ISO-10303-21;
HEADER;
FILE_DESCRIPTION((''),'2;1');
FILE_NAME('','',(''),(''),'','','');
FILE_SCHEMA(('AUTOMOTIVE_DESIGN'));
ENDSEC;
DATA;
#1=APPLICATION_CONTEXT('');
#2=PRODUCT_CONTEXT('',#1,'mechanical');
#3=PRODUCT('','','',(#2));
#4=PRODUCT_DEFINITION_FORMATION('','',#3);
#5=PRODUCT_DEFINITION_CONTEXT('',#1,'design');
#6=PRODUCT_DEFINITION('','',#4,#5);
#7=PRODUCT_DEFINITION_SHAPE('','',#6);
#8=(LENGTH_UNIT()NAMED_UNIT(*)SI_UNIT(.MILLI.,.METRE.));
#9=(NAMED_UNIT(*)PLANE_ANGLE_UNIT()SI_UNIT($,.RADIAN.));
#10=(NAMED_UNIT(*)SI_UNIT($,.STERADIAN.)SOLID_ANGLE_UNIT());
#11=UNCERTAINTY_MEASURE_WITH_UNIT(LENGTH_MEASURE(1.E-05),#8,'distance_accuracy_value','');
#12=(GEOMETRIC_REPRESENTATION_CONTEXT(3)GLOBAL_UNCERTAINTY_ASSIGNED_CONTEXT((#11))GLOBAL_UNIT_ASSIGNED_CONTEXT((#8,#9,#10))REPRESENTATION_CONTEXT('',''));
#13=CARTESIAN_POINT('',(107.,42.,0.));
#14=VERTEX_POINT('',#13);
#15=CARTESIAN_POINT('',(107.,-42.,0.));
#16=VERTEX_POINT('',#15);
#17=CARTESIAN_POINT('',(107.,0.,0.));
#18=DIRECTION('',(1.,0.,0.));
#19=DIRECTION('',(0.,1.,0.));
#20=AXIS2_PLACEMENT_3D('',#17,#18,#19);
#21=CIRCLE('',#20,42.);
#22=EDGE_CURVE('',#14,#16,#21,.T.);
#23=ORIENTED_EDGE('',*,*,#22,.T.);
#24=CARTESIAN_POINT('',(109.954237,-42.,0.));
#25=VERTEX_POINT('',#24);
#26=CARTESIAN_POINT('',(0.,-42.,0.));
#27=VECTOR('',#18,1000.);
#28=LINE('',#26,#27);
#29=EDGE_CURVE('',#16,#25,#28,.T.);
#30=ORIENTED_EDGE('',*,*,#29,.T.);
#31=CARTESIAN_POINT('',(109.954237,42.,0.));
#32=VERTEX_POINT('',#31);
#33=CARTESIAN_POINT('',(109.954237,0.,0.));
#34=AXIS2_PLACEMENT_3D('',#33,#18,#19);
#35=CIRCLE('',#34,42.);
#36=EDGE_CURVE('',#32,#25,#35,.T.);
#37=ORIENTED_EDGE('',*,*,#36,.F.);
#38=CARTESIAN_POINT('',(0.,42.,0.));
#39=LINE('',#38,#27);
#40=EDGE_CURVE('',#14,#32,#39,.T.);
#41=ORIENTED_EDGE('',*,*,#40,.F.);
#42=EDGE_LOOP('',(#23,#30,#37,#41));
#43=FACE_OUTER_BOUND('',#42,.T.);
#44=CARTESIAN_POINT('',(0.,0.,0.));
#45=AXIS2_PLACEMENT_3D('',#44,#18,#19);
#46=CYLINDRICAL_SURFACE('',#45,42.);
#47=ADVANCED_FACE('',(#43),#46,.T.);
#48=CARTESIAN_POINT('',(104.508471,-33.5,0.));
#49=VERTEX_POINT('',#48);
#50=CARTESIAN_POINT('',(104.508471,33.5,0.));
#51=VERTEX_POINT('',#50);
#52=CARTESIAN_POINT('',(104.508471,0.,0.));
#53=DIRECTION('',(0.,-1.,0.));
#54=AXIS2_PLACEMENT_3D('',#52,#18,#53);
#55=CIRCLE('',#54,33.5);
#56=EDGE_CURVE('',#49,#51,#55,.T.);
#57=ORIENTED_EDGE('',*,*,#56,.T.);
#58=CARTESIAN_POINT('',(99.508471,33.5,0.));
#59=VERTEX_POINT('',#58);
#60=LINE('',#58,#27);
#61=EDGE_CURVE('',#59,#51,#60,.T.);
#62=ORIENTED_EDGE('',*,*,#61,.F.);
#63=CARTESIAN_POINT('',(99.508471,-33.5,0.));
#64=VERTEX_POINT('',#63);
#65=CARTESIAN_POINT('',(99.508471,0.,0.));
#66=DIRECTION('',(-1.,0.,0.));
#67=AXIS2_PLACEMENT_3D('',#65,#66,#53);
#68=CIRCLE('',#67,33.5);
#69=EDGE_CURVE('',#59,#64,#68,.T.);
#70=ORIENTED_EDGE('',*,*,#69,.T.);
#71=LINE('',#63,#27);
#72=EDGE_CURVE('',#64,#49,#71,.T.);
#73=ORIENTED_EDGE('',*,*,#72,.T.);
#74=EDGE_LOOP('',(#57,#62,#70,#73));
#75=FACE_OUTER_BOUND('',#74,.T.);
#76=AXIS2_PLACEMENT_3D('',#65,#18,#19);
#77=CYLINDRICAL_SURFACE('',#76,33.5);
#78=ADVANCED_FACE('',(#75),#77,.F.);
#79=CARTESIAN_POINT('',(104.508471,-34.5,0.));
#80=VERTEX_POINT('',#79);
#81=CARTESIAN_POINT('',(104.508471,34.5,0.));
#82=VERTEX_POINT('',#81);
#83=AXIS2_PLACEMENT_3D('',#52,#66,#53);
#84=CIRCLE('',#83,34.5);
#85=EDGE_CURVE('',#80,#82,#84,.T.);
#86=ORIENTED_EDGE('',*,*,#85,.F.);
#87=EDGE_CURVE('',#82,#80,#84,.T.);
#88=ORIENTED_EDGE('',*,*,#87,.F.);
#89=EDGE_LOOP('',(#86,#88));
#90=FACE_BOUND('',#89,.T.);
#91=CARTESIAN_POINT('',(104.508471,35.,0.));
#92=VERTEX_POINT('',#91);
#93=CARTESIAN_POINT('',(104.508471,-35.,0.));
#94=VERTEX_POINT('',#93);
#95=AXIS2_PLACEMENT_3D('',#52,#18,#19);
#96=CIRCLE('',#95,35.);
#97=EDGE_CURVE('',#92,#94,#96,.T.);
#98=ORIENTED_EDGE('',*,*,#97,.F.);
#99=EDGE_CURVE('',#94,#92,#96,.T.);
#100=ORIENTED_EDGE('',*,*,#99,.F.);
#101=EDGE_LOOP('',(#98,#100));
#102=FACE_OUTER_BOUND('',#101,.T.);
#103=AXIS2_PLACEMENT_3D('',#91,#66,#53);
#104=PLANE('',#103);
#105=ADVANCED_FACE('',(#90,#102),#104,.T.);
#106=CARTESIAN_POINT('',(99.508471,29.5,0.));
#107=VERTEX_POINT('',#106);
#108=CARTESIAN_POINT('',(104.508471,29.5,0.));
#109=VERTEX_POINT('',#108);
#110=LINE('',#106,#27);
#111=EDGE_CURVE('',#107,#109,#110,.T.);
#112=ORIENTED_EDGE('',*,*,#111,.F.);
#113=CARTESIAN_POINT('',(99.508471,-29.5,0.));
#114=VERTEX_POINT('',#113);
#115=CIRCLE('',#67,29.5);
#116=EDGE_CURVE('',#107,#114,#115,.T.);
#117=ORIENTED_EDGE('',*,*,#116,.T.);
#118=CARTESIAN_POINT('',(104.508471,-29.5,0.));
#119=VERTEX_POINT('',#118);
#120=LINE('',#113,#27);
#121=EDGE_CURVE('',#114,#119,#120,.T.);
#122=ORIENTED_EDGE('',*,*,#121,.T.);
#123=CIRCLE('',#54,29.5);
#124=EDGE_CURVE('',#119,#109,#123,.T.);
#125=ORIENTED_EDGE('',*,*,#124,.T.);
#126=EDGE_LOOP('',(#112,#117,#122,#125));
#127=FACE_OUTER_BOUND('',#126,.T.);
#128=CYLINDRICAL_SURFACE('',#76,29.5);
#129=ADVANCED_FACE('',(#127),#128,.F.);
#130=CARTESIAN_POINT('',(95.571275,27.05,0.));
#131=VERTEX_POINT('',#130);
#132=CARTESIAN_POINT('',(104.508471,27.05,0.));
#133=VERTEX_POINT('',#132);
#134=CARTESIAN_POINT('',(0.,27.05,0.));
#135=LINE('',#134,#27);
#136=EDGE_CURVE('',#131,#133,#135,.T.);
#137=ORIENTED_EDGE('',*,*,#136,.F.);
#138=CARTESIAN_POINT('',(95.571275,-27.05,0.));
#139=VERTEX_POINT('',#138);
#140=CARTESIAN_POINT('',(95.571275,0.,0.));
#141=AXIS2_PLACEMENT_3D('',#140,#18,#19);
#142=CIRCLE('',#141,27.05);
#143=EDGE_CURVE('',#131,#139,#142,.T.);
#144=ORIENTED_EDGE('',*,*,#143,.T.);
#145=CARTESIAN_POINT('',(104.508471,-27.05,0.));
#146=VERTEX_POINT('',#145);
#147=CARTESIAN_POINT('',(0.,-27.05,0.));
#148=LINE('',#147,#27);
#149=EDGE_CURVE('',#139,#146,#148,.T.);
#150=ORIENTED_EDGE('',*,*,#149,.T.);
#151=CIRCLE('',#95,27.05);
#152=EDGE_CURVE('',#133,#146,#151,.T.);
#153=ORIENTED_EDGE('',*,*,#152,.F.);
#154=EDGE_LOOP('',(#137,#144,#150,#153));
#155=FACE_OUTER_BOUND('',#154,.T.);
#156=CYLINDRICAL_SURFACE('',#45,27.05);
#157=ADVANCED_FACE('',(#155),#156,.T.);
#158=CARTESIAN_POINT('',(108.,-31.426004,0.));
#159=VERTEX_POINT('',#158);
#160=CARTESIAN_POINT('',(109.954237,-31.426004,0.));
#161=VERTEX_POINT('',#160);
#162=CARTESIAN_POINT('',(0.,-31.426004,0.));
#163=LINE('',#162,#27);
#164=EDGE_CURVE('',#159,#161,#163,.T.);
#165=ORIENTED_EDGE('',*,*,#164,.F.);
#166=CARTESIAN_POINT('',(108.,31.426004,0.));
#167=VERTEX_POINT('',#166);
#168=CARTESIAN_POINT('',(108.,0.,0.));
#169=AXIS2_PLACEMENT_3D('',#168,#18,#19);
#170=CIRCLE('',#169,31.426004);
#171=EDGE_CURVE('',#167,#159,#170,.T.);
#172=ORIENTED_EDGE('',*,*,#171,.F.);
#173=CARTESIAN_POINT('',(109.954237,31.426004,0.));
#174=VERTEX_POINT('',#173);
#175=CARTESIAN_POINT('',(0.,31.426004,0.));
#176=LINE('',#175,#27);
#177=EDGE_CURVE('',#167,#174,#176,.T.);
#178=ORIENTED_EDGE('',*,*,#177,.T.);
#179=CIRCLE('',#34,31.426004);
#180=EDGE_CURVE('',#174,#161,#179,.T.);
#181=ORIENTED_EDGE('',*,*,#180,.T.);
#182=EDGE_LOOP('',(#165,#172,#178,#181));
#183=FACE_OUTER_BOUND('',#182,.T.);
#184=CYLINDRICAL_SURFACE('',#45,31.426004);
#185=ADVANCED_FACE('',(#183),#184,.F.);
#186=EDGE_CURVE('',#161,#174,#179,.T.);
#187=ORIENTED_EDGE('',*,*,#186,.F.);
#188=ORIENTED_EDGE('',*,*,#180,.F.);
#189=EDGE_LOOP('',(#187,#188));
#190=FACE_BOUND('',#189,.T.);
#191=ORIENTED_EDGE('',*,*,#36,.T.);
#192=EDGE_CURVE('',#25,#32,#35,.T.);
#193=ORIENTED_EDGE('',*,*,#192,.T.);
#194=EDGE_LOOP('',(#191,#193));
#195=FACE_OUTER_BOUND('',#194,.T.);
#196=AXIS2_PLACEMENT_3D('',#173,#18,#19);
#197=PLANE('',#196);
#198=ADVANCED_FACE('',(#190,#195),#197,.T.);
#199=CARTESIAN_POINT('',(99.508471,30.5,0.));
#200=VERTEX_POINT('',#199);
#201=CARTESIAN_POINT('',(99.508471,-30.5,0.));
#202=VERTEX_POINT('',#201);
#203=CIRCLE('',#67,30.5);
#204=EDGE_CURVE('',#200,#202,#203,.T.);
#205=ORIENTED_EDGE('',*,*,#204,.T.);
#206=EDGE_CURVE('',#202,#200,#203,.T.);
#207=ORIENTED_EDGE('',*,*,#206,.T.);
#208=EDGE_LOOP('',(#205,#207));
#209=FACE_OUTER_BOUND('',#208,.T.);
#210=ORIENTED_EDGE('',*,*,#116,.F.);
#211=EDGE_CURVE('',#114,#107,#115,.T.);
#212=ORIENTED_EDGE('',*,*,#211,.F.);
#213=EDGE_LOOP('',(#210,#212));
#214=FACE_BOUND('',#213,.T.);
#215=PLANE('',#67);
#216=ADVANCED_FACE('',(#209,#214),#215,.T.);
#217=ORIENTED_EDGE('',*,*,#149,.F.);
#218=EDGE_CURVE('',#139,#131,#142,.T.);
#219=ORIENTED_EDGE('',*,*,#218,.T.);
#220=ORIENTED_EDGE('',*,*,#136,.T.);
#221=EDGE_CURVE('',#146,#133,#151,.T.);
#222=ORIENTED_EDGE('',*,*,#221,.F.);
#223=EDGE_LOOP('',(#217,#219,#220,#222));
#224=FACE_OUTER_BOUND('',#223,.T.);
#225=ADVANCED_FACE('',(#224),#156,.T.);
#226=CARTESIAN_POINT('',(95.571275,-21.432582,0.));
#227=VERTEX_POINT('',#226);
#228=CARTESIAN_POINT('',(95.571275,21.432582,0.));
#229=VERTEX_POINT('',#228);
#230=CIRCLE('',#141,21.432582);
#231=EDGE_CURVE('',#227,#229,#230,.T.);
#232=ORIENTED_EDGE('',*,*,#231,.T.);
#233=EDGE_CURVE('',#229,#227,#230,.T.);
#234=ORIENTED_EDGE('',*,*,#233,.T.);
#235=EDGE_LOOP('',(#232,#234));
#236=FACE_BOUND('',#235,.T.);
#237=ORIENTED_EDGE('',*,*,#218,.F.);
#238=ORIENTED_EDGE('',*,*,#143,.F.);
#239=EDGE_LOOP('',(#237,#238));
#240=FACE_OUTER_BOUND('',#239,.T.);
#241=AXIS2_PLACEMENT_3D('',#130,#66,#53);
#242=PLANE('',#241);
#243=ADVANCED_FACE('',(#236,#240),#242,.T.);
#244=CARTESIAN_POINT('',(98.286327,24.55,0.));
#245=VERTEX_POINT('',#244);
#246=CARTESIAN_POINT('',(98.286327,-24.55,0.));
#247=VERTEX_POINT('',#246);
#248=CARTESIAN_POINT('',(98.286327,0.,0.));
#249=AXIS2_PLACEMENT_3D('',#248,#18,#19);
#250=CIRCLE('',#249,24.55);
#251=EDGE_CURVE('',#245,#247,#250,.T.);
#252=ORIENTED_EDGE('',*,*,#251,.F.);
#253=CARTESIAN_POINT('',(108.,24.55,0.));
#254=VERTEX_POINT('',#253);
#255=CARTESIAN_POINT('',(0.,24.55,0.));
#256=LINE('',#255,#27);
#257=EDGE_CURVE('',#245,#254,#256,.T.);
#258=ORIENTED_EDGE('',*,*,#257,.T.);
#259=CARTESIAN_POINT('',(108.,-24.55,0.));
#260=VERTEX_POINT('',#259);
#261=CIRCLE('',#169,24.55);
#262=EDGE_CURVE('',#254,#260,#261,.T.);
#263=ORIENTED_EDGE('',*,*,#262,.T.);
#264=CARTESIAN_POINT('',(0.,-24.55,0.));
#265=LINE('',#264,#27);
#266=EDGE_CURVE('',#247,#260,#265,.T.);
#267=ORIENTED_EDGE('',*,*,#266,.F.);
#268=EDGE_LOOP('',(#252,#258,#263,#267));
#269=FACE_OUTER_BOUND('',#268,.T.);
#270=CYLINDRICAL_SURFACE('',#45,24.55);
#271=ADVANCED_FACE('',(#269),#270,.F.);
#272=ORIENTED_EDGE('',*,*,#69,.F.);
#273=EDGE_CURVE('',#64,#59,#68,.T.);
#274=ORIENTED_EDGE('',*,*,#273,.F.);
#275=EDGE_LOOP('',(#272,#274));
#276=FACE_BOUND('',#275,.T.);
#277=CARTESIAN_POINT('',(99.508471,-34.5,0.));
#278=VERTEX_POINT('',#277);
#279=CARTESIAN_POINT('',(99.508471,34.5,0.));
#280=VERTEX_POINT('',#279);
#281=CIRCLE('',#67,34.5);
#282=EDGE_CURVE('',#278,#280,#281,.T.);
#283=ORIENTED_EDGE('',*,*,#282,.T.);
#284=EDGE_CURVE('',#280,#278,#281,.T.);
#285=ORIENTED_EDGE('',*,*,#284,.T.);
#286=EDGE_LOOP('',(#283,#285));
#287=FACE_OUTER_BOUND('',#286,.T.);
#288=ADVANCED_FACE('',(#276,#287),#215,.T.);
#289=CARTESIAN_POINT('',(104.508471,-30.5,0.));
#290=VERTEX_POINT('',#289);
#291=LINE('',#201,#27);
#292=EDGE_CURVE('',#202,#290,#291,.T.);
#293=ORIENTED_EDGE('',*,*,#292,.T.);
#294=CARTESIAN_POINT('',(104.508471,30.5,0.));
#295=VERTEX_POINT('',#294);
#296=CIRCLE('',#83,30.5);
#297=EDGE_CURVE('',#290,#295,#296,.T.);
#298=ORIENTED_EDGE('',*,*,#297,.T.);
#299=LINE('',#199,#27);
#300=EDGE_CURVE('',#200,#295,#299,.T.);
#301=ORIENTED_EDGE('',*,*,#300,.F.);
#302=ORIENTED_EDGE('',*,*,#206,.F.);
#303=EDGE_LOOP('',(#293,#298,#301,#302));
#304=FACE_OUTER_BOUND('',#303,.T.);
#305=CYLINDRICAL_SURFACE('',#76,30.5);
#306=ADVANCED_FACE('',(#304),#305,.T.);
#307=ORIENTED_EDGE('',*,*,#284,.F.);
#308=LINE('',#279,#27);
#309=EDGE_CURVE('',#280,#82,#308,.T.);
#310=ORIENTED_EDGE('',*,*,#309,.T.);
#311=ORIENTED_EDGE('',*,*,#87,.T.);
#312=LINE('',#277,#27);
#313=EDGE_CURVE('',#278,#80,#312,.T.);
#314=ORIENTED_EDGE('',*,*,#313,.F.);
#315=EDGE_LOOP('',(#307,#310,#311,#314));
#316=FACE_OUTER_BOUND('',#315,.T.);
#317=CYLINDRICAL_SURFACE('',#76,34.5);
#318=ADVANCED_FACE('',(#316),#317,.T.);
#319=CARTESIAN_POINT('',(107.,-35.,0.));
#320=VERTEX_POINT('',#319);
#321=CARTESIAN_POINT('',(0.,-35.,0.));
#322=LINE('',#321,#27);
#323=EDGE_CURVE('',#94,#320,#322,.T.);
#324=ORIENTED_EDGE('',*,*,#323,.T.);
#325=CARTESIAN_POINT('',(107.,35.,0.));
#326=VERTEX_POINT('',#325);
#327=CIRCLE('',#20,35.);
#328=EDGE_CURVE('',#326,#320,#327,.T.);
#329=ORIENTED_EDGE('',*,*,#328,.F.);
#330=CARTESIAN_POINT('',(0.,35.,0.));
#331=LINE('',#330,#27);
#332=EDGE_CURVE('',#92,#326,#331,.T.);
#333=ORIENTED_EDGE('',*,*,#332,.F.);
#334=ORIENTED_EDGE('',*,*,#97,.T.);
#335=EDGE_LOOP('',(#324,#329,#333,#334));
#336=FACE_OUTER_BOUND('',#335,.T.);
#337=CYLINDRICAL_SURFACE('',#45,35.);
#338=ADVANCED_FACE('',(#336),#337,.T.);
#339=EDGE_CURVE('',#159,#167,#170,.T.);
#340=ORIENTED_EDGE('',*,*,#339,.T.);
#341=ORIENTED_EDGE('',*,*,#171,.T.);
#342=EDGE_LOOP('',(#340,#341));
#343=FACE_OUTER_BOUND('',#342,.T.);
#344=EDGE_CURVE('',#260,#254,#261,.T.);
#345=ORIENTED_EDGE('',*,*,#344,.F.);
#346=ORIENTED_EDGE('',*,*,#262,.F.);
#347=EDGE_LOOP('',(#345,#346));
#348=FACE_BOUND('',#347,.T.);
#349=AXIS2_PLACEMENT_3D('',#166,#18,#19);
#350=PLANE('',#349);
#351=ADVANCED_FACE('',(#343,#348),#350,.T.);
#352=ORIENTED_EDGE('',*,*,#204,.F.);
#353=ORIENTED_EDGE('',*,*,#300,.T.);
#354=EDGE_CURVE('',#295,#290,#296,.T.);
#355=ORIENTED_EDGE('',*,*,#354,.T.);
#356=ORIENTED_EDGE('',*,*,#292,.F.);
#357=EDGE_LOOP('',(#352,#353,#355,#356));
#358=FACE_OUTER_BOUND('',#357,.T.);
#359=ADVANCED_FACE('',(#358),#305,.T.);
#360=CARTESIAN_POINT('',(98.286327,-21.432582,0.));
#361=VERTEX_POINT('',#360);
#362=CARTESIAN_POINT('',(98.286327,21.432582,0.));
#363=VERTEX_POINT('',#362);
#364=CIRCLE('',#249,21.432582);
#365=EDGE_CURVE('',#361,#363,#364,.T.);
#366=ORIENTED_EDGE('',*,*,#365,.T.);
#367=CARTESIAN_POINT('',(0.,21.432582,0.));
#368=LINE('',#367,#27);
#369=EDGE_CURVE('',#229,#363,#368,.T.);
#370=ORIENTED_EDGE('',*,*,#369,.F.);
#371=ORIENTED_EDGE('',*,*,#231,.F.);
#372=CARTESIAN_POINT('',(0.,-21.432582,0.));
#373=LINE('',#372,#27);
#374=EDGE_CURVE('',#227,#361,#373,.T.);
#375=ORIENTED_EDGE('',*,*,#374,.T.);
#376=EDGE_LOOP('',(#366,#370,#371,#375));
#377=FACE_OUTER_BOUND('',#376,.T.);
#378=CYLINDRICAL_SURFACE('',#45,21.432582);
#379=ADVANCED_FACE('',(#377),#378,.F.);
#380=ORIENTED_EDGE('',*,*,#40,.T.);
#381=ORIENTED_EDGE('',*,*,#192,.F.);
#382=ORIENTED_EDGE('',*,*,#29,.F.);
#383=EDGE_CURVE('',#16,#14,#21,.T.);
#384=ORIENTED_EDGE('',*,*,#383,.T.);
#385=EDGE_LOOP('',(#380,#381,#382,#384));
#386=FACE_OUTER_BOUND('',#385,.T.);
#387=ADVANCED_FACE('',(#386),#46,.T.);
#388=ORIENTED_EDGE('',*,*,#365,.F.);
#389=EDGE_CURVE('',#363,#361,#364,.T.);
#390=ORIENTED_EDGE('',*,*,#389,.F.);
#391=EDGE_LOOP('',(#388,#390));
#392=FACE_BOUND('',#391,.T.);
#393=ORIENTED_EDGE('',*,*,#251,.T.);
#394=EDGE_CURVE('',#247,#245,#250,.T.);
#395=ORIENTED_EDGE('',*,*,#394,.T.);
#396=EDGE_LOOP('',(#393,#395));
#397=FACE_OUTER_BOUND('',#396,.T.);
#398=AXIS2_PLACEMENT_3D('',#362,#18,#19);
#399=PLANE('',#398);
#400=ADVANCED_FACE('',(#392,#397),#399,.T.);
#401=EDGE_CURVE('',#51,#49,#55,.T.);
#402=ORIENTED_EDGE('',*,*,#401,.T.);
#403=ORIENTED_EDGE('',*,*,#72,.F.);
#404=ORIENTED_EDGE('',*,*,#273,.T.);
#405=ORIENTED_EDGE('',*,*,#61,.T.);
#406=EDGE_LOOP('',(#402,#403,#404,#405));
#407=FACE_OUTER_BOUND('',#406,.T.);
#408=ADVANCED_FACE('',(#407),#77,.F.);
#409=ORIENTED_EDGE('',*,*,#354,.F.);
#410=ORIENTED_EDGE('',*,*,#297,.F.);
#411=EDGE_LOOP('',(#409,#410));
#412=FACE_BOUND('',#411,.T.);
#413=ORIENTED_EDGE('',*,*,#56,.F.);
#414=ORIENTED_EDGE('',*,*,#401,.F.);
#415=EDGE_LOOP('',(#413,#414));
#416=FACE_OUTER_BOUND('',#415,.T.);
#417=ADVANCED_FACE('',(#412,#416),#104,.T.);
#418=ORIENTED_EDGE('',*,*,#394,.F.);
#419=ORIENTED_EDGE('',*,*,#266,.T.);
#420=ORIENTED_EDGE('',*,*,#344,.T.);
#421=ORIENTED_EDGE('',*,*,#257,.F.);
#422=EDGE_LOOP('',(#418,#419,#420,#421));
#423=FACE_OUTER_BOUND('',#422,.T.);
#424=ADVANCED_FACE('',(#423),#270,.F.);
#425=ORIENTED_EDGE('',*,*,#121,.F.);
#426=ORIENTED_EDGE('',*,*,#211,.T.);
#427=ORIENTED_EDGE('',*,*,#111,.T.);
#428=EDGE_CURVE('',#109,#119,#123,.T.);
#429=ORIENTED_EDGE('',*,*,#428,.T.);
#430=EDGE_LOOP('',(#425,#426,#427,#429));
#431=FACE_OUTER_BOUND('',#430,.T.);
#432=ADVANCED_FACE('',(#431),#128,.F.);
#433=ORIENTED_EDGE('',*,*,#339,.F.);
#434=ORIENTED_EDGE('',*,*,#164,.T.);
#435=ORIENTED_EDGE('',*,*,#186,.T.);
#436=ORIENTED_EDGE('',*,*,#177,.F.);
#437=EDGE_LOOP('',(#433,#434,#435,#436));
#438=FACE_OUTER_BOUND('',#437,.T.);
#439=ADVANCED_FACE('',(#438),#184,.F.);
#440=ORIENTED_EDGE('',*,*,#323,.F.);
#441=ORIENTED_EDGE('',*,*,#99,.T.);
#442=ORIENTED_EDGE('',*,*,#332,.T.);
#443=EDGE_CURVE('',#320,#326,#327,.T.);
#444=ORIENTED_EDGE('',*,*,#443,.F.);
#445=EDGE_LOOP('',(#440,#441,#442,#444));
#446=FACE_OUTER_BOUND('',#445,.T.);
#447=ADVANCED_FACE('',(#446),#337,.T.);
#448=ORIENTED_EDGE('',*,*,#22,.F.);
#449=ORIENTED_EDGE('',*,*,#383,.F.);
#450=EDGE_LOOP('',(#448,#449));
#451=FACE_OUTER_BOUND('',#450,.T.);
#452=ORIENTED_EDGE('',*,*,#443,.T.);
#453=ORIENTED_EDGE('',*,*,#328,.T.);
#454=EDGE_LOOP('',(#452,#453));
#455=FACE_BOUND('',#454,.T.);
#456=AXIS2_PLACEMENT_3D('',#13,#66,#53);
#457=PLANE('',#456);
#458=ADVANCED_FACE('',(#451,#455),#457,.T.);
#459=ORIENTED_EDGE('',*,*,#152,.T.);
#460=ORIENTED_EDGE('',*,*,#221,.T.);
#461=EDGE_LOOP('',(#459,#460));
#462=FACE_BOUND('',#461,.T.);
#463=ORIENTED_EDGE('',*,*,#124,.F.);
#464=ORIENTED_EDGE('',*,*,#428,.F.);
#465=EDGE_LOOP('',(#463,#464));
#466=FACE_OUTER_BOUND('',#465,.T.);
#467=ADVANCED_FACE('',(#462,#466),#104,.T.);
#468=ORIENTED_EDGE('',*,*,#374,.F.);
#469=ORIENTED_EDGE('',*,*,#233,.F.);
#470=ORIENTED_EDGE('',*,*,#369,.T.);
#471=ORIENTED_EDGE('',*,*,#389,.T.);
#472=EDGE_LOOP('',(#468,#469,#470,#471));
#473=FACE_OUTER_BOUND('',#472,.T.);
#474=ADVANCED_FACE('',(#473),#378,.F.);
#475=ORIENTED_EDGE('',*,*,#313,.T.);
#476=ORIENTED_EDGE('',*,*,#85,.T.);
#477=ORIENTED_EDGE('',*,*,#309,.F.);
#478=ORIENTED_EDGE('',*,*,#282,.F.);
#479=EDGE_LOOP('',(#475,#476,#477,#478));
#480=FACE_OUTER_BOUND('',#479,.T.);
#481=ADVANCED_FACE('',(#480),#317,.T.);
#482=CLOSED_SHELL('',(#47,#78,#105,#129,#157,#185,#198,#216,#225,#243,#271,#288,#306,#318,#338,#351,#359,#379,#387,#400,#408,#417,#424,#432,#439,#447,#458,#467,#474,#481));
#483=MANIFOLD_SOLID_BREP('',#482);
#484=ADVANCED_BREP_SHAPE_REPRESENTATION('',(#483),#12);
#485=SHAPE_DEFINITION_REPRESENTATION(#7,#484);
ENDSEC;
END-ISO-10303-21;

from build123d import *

# Parameters (mm, degrees)
SKETCH2_R           = 34.5
SKETCH2_R_2         = 33.5
SKETCH2_R_3         = 30.5
SKETCH2_R_4         = 29.5
BOSS_EXTRUDE1_DEPTH = 5


with BuildPart() as part:
    # Sketch1 → Revolve1 (revolve)
    with BuildSketch(Plane.XY):
        Polygon((107, 42), (107, 35), (104.508470742, 35), (104.508470742, 27.05), (95.571275451, 27.05), (95.571275451, 21.43258158), (98.286326817, 21.43258158), (98.286326817, 24.55), (108, 24.55), (108, 31.426003585), (109.954236571, 31.426003585), (109.954236571, 42), align=None)
    revolve(axis=Axis((0, 0, 0), (-1, 0, 0)))

    # Sketch2 → Boss-Extrude1 (add)
    # profile 1 of 2: a face of its own
    with BuildSketch(Plane.ZY.offset(-104.508470742)):
        with Locations(Location((0, 0, 0), (0, 0, 270))):
            Circle(SKETCH2_R)
        with Locations(Location((0, 0, 0), (0, 0, 270))):
            Circle(SKETCH2_R_2, mode=Mode.SUBTRACT)
    # profile 2 of 2: a face of its own
    with BuildSketch(Plane.ZY.offset(-104.508470742)):
        with Locations(Location((0, 0, 0), (0, 0, 270))):
            Circle(SKETCH2_R_3)
        with Locations(Location((0, 0, 0), (0, 0, 270))):
            Circle(SKETCH2_R_4, mode=Mode.SUBTRACT)
    extrude(amount=BOSS_EXTRUDE1_DEPTH)


solid = part.part
